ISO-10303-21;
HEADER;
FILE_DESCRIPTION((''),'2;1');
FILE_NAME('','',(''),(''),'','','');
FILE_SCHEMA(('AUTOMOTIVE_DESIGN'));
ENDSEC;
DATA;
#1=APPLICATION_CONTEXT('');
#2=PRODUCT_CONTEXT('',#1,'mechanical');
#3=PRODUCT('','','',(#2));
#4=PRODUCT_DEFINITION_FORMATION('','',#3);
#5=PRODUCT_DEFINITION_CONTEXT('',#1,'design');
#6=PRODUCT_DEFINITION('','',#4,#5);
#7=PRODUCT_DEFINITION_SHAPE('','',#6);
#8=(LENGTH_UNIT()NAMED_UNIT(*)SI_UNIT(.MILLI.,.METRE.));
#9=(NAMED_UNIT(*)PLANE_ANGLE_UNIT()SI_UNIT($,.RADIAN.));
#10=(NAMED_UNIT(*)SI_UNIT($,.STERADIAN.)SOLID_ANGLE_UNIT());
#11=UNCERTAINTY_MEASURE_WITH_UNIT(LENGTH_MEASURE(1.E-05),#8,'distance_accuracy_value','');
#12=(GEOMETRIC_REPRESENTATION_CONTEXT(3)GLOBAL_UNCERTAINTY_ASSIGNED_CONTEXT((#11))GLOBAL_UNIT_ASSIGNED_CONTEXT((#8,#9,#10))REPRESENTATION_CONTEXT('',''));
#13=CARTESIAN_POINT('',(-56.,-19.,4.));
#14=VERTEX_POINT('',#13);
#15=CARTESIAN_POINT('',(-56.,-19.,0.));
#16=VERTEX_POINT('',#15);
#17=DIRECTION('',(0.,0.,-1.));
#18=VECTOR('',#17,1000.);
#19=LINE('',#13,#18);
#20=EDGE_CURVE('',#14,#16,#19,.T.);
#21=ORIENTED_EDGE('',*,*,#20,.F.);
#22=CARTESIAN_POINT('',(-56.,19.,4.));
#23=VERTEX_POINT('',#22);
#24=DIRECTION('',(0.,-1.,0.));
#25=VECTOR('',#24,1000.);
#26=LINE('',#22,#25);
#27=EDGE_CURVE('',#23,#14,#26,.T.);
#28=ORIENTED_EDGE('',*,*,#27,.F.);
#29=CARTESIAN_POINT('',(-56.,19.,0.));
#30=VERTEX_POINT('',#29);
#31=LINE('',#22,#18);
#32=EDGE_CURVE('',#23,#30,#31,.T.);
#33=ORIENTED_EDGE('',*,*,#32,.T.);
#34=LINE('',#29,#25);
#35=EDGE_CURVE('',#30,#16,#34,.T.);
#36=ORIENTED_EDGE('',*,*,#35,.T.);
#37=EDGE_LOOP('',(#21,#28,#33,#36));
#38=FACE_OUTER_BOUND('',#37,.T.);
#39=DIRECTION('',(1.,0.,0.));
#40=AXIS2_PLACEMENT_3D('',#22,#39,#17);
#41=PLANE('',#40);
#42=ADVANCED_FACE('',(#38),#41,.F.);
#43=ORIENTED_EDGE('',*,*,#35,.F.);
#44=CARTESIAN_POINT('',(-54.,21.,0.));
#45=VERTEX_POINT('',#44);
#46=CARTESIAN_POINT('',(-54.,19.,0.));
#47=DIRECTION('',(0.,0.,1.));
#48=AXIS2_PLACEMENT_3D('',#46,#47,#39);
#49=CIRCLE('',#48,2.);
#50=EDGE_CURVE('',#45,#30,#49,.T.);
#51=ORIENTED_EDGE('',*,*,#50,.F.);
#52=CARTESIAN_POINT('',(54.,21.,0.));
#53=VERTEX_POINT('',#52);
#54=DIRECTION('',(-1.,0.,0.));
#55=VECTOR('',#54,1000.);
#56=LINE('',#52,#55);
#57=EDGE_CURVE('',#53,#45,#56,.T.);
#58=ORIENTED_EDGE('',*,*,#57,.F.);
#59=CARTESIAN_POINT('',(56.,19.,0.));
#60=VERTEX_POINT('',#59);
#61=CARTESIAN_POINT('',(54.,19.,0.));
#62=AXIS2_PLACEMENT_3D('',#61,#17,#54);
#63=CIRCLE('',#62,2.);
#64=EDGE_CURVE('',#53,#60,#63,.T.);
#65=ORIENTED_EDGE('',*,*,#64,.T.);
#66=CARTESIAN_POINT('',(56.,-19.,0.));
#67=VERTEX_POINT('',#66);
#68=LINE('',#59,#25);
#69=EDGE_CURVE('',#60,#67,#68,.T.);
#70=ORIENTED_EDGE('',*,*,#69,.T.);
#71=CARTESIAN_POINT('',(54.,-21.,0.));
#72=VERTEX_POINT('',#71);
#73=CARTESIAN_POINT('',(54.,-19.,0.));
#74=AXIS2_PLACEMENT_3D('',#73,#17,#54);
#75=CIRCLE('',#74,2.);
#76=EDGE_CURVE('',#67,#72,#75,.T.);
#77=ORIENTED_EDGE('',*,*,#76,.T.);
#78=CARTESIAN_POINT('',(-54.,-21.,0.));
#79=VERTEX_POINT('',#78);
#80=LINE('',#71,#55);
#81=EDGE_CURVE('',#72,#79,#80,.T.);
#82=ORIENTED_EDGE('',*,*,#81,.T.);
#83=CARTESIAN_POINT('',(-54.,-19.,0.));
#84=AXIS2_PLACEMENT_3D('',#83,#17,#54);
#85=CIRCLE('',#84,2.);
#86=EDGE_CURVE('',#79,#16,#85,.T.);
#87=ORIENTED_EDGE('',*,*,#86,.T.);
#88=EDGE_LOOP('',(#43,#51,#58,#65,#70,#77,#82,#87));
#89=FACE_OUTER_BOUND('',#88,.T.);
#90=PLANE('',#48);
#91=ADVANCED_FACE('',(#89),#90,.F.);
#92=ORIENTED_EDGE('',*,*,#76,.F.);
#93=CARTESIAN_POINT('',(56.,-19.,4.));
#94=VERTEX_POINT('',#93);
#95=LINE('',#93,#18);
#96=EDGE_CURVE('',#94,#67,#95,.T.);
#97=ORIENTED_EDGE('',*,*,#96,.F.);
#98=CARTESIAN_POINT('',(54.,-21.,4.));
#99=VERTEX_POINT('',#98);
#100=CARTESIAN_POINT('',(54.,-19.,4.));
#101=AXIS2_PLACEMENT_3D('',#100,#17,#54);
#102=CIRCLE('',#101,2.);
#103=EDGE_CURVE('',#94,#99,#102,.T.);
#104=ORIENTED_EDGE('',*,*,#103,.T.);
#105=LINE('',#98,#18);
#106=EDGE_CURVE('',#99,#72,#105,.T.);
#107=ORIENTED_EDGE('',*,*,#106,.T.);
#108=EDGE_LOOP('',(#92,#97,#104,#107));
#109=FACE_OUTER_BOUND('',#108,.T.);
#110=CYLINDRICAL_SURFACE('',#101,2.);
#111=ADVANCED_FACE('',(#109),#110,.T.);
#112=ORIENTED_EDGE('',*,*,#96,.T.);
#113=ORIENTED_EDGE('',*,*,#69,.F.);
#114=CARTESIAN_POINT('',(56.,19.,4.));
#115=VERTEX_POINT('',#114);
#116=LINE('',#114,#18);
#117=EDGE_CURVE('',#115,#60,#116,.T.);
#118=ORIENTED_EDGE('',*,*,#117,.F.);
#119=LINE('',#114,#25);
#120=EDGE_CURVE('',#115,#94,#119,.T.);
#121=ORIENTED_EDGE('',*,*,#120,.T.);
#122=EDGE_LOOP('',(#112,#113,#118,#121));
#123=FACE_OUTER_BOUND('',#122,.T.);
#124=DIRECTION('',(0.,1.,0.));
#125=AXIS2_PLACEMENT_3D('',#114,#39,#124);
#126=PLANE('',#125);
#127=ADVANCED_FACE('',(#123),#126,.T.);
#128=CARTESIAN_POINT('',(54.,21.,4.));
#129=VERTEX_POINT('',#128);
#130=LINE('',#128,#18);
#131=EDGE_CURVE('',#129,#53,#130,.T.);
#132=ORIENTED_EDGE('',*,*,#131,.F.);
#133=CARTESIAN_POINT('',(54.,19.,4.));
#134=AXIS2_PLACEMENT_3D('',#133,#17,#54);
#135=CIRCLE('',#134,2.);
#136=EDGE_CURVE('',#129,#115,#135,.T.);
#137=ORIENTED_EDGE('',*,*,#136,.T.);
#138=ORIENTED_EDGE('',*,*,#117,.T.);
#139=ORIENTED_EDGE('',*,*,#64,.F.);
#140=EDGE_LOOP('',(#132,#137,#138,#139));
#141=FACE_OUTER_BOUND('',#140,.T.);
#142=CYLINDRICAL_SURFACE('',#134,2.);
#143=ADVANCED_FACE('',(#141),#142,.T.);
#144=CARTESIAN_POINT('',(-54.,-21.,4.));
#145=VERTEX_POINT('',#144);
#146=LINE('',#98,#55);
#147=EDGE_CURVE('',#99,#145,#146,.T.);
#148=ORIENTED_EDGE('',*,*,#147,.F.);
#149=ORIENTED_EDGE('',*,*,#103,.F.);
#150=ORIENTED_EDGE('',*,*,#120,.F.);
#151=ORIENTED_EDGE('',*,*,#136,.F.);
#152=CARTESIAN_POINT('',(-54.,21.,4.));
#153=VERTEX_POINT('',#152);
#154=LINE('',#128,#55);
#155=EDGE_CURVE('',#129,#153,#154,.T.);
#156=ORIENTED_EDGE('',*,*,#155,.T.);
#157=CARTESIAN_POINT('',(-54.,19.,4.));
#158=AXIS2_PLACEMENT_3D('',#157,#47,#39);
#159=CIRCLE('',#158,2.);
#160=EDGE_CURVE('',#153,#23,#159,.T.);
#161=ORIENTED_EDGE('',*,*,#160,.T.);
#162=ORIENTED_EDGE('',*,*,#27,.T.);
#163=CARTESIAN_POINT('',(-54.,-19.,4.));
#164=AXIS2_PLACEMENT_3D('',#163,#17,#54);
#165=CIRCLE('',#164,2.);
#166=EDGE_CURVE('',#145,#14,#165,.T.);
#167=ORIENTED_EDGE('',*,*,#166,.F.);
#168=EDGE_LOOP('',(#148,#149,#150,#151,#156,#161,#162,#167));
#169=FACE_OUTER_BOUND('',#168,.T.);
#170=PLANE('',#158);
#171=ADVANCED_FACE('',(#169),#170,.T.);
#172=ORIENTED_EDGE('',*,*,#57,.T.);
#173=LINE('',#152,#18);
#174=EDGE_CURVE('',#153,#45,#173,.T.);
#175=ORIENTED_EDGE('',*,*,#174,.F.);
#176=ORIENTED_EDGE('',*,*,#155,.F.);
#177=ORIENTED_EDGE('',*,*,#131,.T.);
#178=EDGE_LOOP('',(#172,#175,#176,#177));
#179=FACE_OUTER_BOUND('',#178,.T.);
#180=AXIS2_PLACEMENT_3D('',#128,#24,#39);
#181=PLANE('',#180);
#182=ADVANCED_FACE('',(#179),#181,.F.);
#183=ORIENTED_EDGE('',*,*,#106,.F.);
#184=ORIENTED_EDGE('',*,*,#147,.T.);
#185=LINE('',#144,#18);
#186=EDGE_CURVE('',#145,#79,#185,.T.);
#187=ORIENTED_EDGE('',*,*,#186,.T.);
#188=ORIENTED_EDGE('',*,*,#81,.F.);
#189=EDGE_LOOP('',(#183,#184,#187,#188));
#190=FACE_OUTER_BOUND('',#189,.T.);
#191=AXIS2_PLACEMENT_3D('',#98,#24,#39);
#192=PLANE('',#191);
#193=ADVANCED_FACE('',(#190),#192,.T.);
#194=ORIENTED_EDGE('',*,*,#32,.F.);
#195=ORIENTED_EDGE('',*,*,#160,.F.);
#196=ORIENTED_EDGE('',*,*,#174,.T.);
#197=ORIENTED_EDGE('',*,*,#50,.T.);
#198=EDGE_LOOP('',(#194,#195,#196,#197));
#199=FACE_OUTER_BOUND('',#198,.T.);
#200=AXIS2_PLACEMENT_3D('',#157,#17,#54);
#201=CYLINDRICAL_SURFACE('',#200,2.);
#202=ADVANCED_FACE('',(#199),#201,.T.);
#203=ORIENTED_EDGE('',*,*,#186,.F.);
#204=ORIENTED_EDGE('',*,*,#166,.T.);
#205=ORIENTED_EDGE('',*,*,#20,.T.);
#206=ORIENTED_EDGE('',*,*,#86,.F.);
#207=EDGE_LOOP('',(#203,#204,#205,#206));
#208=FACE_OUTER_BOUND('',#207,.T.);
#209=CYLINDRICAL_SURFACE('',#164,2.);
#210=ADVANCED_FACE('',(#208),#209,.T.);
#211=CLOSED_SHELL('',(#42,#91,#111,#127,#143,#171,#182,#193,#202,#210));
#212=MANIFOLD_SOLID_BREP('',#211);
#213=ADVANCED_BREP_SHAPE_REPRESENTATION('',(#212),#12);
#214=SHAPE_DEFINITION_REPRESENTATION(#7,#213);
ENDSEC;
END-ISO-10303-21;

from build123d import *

# Parameters (mm, degrees)
BOSS_EXTRUDE1_DEPTH = 4


with BuildPart() as part:
    # Sketch1 → Boss-Extrude1 (new body)
    with BuildSketch(Plane.XY):
        with BuildLine():
            Line((54, 21), (-54, 21))
            ThreePointArc((-54, 21), (-55.414213562, 20.414213562), (-56, 19))
            Line((-56, 19), (-56, -19))
            ThreePointArc((-56, -19), (-55.414213562, -20.414213562), (-54, -21))
            Line((-54, -21), (54, -21))
            ThreePointArc((54, -21), (55.414213562, -20.414213562), (56, -19))
            Line((56, -19), (56, 19))
            ThreePointArc((56, 19), (55.414213562, 20.414213562), (54, 21))
        make_face()
    extrude(amount=BOSS_EXTRUDE1_DEPTH)


solid = part.part
